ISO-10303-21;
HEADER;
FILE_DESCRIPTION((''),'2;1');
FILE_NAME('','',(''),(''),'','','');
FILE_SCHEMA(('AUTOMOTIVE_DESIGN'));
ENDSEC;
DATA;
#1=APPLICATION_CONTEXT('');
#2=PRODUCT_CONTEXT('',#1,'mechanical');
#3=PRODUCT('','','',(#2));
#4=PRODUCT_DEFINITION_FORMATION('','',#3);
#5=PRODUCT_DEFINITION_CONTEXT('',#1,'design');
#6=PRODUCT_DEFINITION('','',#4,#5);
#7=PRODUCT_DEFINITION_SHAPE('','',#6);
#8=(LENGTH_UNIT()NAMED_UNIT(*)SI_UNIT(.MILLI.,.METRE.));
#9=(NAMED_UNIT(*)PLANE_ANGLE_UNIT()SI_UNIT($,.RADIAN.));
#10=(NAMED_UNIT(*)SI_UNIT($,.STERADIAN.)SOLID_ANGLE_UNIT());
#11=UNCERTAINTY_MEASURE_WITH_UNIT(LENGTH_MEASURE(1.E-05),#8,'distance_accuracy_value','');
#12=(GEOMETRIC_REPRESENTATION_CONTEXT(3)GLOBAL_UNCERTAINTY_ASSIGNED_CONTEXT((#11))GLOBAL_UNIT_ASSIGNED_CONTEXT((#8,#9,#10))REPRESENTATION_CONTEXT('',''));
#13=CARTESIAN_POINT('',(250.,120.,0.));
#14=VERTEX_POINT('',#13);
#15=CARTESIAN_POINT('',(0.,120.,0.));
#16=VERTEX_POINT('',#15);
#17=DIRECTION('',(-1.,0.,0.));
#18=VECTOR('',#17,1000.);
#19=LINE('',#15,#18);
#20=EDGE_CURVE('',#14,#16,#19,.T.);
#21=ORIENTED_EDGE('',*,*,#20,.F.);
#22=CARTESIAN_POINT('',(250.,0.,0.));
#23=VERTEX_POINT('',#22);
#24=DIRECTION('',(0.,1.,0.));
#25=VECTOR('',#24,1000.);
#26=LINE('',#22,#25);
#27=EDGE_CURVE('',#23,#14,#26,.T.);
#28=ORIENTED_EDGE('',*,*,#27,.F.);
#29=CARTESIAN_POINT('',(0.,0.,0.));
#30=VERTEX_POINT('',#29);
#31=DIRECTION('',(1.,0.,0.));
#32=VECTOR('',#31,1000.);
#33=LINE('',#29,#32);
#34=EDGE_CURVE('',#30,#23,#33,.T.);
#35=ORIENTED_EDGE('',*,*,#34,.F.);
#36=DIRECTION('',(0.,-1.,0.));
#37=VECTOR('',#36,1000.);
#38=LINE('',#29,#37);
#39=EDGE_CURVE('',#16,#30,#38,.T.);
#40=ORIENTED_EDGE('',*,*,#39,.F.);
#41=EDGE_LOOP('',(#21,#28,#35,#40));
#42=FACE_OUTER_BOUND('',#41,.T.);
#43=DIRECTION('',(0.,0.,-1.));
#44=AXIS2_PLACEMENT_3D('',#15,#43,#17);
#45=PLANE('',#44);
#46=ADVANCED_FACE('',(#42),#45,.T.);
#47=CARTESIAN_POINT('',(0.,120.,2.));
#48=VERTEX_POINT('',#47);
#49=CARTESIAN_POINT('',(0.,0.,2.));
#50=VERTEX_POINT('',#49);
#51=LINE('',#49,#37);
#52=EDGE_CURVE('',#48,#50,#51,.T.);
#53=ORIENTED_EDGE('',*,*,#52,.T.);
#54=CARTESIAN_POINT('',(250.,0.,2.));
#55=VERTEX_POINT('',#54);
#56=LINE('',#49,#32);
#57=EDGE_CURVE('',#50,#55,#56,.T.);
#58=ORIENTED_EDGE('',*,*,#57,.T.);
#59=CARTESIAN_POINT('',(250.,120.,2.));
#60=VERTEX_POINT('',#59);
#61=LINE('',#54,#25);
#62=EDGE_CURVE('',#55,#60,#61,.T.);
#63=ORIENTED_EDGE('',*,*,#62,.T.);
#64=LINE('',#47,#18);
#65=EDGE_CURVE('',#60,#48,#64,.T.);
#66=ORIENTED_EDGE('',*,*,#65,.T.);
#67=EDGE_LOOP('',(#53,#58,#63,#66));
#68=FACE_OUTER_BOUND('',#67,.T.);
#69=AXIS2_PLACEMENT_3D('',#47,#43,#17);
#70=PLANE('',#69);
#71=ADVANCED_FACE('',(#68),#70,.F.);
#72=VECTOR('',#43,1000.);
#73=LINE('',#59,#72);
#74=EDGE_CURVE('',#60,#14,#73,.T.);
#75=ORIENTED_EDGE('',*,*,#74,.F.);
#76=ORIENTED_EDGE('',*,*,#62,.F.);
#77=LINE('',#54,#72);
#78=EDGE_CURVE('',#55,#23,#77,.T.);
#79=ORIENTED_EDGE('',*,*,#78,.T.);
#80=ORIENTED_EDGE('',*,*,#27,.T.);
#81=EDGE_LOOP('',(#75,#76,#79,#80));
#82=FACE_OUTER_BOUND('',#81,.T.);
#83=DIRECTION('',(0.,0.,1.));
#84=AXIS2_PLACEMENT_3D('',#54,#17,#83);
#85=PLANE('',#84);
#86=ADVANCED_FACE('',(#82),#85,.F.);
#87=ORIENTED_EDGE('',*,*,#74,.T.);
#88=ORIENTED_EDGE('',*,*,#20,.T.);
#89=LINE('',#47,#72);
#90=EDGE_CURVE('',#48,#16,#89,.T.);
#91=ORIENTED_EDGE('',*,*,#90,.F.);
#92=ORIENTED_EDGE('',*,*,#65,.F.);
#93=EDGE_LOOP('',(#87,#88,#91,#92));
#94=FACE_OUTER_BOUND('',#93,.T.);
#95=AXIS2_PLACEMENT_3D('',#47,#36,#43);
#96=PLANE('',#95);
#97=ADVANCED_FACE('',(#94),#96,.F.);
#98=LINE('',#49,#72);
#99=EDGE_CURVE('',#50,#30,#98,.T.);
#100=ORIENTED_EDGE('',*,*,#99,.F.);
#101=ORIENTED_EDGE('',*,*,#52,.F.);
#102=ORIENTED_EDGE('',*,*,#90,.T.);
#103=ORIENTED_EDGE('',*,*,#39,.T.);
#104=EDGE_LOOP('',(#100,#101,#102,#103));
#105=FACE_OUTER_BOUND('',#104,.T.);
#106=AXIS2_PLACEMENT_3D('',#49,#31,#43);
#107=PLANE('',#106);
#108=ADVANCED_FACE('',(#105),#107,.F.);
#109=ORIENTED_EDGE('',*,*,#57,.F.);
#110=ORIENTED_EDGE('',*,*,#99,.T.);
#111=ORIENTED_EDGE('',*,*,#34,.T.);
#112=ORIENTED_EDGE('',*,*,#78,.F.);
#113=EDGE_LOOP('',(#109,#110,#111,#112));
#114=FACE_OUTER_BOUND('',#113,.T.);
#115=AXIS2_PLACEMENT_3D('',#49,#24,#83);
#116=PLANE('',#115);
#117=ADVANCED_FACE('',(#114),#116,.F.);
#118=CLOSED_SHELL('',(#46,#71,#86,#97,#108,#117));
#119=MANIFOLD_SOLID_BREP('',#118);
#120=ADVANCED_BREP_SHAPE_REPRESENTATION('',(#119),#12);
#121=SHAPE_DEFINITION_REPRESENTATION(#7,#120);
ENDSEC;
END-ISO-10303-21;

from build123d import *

# Parameters (mm, degrees)
SKETCH1_W           = 250
SKETCH1_H           = 120
BOSS_EXTRUDE1_DEPTH = 2


with BuildPart() as part:
    # Sketch1 → Boss-Extrude1 (new body)
    with BuildSketch(Plane.XY):
        with Locations((125, 60)):
            Rectangle(SKETCH1_W, SKETCH1_H)
    extrude(amount=BOSS_EXTRUDE1_DEPTH)


solid = part.part
